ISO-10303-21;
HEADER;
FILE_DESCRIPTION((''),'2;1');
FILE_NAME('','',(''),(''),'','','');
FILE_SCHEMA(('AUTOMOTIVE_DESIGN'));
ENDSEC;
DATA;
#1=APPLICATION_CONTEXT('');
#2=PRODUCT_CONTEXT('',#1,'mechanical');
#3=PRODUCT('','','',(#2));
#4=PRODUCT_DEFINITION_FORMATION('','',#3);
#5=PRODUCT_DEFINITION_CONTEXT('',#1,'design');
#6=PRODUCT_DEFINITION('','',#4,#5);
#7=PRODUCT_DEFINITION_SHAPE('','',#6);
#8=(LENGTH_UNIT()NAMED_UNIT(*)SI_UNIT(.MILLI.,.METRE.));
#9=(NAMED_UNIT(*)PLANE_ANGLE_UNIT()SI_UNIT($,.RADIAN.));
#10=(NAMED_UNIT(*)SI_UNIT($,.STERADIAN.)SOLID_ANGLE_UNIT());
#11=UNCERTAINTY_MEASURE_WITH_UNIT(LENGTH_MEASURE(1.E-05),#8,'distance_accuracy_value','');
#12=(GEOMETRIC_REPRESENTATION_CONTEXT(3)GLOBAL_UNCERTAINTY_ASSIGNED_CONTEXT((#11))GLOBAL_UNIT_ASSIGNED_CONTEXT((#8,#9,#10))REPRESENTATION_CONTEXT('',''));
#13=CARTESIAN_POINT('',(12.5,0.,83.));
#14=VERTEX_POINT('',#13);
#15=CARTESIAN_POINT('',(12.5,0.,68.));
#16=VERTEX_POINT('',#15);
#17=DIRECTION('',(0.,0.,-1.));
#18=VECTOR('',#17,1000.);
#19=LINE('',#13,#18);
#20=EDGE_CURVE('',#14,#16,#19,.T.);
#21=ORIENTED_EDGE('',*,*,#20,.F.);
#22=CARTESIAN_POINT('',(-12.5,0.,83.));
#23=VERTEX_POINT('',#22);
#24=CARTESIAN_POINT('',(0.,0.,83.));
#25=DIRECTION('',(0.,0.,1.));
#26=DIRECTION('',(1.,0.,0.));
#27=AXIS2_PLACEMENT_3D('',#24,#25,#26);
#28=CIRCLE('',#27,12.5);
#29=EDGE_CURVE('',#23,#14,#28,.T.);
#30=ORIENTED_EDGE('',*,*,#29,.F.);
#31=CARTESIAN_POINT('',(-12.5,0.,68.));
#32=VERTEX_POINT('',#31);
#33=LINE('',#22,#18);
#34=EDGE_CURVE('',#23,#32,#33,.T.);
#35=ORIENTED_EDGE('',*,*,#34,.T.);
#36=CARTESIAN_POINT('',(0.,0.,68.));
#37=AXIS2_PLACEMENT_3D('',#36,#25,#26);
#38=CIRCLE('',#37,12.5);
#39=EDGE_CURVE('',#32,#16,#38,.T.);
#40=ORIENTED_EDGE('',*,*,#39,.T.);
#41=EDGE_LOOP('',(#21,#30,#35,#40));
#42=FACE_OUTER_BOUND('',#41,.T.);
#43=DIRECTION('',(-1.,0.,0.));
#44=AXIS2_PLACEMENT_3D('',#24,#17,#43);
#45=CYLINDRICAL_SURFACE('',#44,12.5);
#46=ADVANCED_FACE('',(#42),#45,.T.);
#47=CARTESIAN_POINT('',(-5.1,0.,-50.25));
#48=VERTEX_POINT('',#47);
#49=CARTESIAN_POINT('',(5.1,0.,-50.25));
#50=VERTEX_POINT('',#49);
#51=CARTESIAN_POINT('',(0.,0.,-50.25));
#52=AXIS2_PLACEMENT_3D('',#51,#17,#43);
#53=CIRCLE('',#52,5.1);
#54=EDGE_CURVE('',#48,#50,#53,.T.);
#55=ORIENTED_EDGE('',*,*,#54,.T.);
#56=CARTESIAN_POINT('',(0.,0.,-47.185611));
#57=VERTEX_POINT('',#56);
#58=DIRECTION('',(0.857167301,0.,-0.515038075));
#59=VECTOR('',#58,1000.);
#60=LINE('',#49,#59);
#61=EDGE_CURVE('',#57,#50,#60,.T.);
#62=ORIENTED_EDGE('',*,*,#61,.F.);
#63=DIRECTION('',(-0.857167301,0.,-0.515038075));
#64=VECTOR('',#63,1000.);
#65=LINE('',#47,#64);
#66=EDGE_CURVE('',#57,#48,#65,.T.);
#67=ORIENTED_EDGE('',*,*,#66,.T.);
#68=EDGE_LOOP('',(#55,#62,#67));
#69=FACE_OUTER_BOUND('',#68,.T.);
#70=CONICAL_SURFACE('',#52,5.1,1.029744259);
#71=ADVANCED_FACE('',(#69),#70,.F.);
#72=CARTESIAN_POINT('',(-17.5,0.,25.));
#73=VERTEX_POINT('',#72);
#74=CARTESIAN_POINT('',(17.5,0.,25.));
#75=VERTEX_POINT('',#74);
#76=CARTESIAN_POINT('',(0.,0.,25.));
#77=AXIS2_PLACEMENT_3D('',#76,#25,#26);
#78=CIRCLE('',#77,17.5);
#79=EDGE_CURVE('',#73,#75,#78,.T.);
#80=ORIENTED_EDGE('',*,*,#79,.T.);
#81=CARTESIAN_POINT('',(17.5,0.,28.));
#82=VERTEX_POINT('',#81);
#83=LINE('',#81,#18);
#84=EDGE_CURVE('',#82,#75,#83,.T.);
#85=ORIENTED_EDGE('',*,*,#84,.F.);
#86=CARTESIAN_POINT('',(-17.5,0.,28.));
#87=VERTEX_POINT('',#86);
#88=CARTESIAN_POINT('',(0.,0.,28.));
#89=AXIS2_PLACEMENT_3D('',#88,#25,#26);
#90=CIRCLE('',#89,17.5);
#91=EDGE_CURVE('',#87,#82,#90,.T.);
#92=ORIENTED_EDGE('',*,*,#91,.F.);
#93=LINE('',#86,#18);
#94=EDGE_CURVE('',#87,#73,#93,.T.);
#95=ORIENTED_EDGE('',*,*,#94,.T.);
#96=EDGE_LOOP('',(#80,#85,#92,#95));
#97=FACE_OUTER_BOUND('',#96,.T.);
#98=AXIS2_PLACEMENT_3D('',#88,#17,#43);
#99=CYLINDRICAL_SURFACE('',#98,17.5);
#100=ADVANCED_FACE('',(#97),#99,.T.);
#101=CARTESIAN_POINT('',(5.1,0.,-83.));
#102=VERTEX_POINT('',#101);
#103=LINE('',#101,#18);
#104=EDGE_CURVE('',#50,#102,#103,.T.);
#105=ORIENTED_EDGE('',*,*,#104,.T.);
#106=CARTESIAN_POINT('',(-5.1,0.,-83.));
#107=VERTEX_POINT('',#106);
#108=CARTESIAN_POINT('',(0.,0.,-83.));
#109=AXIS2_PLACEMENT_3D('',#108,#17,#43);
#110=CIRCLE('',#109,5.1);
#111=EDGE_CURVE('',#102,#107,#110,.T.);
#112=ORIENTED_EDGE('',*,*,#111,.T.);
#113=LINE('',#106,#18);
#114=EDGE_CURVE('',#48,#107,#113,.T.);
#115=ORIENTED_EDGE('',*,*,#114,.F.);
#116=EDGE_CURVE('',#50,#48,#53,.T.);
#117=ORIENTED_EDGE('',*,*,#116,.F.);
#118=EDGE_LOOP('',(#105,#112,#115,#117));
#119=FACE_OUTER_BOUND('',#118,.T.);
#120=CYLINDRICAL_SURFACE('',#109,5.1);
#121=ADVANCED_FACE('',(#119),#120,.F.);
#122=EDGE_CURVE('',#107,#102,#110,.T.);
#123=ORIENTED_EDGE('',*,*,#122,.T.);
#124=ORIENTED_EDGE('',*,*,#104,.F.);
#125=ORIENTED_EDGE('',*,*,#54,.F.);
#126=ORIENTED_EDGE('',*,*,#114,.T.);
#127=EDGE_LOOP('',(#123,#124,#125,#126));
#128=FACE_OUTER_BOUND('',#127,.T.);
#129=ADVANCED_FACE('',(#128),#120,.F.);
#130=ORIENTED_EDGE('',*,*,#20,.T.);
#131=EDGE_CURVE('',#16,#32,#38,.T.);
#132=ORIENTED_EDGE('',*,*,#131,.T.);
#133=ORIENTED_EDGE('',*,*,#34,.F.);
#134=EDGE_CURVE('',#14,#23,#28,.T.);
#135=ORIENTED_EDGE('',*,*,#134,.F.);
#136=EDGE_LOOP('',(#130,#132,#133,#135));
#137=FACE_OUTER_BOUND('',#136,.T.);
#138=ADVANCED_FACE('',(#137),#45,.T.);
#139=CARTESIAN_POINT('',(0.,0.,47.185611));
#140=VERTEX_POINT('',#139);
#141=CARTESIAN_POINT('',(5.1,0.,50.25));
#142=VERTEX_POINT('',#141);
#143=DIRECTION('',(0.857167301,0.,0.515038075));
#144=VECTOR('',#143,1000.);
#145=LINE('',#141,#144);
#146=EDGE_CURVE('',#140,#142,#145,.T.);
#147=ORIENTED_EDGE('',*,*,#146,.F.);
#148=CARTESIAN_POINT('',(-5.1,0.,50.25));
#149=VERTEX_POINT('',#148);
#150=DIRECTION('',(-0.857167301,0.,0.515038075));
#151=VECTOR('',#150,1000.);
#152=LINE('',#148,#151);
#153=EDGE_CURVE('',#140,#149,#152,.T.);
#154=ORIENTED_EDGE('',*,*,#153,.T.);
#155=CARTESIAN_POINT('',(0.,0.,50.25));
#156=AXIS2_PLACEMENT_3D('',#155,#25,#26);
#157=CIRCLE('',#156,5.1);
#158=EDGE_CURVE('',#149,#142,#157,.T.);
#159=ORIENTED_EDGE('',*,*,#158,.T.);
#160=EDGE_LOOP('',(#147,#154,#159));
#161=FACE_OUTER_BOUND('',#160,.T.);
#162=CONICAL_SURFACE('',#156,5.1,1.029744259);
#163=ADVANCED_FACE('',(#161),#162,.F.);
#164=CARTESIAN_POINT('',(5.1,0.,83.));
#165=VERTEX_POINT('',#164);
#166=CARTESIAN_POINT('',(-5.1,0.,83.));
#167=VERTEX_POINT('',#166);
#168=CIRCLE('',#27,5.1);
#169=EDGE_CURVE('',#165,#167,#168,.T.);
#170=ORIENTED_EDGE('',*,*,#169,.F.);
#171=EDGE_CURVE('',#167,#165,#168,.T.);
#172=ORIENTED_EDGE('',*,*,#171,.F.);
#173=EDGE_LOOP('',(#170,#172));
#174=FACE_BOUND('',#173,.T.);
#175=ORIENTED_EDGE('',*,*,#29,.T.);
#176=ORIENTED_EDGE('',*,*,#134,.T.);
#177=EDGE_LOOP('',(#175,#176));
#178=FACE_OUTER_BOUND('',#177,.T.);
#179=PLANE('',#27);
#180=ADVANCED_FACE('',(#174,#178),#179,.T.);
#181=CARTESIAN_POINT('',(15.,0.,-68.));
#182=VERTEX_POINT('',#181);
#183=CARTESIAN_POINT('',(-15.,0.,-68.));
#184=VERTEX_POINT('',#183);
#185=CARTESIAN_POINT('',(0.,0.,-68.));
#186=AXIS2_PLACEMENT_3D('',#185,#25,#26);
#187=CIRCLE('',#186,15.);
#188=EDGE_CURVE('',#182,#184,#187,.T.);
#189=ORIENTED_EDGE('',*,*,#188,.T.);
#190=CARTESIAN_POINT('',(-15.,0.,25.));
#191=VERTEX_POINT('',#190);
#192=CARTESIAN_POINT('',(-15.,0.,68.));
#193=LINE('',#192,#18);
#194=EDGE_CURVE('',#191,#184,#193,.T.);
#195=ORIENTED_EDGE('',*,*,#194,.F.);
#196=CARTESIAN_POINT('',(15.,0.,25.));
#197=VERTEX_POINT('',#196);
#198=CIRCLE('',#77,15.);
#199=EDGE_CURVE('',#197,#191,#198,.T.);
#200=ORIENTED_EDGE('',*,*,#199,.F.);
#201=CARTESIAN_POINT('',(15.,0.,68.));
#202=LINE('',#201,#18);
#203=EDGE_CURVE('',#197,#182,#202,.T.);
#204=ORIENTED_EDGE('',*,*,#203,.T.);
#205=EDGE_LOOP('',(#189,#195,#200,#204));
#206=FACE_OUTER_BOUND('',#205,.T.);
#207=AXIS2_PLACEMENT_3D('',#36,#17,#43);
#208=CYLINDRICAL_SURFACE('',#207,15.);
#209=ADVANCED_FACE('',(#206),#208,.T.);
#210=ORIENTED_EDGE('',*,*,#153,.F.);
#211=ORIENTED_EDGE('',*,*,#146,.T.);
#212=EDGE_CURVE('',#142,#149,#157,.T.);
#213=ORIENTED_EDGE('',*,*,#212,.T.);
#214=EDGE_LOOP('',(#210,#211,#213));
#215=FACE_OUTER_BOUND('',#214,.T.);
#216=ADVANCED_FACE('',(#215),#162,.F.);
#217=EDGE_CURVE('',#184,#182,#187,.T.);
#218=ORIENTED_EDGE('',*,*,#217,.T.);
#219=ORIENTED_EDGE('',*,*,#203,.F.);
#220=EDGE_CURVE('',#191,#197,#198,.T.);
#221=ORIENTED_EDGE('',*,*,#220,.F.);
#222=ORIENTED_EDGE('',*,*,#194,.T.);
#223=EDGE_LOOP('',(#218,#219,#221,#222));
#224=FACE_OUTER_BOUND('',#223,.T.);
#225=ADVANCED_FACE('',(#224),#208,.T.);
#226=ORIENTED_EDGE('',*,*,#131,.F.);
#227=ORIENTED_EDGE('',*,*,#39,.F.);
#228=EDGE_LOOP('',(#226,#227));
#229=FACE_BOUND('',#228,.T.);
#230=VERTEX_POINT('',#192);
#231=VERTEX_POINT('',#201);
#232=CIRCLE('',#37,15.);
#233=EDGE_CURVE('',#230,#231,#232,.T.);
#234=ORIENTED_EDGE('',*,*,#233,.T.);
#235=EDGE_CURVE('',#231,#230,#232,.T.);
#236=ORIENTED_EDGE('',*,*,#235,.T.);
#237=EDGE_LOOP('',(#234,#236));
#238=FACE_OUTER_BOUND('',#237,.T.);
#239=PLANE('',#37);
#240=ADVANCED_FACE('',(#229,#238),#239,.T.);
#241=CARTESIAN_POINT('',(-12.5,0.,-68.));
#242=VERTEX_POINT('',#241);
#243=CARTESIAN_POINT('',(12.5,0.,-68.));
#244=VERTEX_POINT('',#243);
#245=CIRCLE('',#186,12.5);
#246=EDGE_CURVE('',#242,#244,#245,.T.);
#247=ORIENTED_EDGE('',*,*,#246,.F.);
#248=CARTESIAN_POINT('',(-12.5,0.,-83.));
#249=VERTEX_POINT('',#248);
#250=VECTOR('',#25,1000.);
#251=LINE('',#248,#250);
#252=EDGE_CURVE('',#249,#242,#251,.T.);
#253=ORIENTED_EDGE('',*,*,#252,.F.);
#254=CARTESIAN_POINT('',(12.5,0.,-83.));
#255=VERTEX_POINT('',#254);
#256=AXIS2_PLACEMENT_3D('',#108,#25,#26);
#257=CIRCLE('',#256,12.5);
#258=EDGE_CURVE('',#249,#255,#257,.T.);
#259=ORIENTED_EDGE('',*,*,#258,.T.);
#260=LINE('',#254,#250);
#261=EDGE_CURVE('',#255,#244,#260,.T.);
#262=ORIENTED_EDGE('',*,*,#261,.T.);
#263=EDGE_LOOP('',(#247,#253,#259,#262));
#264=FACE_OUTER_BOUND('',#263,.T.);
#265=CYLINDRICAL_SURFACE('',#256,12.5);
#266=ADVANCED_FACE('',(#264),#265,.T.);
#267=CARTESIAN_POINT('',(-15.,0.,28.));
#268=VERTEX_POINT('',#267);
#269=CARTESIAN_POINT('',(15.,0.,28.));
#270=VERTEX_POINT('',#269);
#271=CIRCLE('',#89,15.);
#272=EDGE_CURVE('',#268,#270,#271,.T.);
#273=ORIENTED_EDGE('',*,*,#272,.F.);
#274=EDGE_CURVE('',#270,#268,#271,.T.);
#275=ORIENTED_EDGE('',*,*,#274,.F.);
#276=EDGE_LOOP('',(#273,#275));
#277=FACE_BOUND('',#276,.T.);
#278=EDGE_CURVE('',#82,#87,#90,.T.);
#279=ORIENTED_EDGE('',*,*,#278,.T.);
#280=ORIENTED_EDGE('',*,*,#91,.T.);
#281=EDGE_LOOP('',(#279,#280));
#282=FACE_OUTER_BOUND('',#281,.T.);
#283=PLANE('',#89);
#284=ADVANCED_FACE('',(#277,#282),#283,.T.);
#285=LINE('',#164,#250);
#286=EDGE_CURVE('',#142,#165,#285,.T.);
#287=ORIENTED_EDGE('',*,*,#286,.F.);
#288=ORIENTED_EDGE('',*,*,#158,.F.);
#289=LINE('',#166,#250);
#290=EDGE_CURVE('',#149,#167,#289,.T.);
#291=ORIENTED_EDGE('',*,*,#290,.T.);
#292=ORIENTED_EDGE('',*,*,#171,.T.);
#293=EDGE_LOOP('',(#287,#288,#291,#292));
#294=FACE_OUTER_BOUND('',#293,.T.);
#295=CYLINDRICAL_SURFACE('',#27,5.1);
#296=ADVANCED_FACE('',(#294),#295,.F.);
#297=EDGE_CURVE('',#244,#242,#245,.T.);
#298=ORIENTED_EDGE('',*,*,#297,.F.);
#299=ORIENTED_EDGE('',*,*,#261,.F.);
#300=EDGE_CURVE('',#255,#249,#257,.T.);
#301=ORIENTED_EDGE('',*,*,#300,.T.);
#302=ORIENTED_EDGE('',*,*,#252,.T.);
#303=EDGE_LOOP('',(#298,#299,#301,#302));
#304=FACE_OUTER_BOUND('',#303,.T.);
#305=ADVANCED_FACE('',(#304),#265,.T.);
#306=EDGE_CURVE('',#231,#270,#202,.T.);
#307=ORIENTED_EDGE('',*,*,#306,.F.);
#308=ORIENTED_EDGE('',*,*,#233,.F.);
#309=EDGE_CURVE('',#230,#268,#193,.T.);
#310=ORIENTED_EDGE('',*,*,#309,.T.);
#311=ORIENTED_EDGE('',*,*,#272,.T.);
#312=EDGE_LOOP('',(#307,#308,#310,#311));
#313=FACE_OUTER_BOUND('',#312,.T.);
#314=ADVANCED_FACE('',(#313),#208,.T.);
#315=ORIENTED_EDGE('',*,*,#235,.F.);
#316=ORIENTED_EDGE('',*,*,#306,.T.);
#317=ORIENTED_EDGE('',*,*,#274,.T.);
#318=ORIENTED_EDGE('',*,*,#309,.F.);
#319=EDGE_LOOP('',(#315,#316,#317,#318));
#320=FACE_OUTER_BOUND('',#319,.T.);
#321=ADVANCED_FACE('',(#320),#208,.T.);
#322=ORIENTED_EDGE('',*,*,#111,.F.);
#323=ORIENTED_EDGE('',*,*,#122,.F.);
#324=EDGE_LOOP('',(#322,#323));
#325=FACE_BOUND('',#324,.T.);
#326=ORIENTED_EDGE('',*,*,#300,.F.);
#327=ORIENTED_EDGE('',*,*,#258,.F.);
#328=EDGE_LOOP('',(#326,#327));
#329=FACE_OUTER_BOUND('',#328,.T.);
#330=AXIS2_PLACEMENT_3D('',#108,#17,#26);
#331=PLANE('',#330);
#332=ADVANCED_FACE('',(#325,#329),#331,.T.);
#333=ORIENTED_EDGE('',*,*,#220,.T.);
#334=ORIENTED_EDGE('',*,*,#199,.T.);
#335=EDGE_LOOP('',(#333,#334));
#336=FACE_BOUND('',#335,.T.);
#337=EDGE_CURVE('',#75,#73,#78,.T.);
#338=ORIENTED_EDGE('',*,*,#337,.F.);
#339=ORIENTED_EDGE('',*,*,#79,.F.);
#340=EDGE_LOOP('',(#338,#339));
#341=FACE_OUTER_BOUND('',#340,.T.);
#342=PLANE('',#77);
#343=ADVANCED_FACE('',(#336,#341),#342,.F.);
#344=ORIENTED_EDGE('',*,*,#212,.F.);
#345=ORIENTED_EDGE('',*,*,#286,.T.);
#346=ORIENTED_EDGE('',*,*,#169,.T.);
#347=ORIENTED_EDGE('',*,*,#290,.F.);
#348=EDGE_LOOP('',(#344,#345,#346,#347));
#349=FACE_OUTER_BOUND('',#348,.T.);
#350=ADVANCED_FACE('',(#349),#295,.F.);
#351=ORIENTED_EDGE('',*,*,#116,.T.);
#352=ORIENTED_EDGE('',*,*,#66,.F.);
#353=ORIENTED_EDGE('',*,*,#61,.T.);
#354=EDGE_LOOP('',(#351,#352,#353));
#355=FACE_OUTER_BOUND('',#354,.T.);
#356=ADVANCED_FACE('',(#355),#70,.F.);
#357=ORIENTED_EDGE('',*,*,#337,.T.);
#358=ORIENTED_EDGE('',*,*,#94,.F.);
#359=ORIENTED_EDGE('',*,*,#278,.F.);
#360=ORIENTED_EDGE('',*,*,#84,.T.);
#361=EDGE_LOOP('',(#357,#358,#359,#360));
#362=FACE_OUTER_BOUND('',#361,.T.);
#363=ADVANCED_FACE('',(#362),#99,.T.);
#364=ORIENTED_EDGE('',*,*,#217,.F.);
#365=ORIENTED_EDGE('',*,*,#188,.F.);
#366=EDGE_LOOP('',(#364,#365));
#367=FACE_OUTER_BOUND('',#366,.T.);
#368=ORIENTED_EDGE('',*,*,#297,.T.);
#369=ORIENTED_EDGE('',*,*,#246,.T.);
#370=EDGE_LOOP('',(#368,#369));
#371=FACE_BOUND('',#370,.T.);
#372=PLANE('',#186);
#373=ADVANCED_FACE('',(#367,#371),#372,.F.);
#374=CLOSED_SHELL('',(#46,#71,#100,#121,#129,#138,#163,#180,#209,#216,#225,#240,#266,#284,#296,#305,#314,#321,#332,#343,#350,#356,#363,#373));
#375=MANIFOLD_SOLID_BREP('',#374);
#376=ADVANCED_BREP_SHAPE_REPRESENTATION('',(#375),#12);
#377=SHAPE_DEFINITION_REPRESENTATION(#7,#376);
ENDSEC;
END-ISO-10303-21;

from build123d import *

# Parameters (mm, degrees)
SKETCH1_R              = 15
BOSS_EXTRUDE1_DEPTH    = 68
SKETCH2_R              = 12.5
BOSS_EXTRUDE2_DEPTH    = 15
BOSS_EXTRUDE4_START    = 25
SKETCH4_R              = 17.5
BOSS_EXTRUDE4_DEPTH    = 3
M12_TAPPED_HOLE1_D     = 10.2
M12_TAPPED_HOLE1_DEPTH = 32.75
M12_TAPPED_HOLE1_TIP   = 3.064389157
M12_TAPPED_HOLE2_D     = 10.2
M12_TAPPED_HOLE2_DEPTH = 32.75
M12_TAPPED_HOLE2_TIP   = 3.064389157


with BuildPart() as part:
    # Sketch1 → Boss-Extrude1 (new, symmetric)
    with BuildSketch(Plane.XY):
        Circle(SKETCH1_R)
    extrude(amount=BOSS_EXTRUDE1_DEPTH, both=True)

    # Sketch2 → Boss-Extrude2 (add)
    with BuildSketch(Plane.XY.offset(68)):
        Circle(SKETCH2_R)
    boss_extrude2 = extrude(amount=BOSS_EXTRUDE2_DEPTH)

    # Mirror1: Boss-Extrude2 across plane
    add(boss_extrude2.mirror(Plane.XY))

    # Sketch4 → Boss-Extrude4 (add)
    with BuildSketch(Plane.XY.offset(BOSS_EXTRUDE4_START)):
        Circle(SKETCH4_R)
    extrude(amount=BOSS_EXTRUDE4_DEPTH)

    # M12 Tapped Hole1
    with Locations(Plane(origin=(0, 0, -83), x_dir=(-1, 0, 0), z_dir=(0, 0, -1))):
        with Locations((0, 0)):
            Hole(M12_TAPPED_HOLE1_D / 2, depth=M12_TAPPED_HOLE1_DEPTH)
            with Locations((0, 0, -(M12_TAPPED_HOLE1_DEPTH + M12_TAPPED_HOLE1_TIP / 2))):  # 118° drill point
                Cone(0, M12_TAPPED_HOLE1_D / 2, M12_TAPPED_HOLE1_TIP, mode=Mode.SUBTRACT)

    # M12 Tapped Hole2
    with Locations(Plane.XY.offset(83)):
        with Locations((0, 0)):
            Hole(M12_TAPPED_HOLE2_D / 2, depth=M12_TAPPED_HOLE2_DEPTH)
            with Locations((0, 0, -(M12_TAPPED_HOLE2_DEPTH + M12_TAPPED_HOLE2_TIP / 2))):  # 118° drill point
                Cone(0, M12_TAPPED_HOLE2_D / 2, M12_TAPPED_HOLE2_TIP, mode=Mode.SUBTRACT)


solid = part.part
